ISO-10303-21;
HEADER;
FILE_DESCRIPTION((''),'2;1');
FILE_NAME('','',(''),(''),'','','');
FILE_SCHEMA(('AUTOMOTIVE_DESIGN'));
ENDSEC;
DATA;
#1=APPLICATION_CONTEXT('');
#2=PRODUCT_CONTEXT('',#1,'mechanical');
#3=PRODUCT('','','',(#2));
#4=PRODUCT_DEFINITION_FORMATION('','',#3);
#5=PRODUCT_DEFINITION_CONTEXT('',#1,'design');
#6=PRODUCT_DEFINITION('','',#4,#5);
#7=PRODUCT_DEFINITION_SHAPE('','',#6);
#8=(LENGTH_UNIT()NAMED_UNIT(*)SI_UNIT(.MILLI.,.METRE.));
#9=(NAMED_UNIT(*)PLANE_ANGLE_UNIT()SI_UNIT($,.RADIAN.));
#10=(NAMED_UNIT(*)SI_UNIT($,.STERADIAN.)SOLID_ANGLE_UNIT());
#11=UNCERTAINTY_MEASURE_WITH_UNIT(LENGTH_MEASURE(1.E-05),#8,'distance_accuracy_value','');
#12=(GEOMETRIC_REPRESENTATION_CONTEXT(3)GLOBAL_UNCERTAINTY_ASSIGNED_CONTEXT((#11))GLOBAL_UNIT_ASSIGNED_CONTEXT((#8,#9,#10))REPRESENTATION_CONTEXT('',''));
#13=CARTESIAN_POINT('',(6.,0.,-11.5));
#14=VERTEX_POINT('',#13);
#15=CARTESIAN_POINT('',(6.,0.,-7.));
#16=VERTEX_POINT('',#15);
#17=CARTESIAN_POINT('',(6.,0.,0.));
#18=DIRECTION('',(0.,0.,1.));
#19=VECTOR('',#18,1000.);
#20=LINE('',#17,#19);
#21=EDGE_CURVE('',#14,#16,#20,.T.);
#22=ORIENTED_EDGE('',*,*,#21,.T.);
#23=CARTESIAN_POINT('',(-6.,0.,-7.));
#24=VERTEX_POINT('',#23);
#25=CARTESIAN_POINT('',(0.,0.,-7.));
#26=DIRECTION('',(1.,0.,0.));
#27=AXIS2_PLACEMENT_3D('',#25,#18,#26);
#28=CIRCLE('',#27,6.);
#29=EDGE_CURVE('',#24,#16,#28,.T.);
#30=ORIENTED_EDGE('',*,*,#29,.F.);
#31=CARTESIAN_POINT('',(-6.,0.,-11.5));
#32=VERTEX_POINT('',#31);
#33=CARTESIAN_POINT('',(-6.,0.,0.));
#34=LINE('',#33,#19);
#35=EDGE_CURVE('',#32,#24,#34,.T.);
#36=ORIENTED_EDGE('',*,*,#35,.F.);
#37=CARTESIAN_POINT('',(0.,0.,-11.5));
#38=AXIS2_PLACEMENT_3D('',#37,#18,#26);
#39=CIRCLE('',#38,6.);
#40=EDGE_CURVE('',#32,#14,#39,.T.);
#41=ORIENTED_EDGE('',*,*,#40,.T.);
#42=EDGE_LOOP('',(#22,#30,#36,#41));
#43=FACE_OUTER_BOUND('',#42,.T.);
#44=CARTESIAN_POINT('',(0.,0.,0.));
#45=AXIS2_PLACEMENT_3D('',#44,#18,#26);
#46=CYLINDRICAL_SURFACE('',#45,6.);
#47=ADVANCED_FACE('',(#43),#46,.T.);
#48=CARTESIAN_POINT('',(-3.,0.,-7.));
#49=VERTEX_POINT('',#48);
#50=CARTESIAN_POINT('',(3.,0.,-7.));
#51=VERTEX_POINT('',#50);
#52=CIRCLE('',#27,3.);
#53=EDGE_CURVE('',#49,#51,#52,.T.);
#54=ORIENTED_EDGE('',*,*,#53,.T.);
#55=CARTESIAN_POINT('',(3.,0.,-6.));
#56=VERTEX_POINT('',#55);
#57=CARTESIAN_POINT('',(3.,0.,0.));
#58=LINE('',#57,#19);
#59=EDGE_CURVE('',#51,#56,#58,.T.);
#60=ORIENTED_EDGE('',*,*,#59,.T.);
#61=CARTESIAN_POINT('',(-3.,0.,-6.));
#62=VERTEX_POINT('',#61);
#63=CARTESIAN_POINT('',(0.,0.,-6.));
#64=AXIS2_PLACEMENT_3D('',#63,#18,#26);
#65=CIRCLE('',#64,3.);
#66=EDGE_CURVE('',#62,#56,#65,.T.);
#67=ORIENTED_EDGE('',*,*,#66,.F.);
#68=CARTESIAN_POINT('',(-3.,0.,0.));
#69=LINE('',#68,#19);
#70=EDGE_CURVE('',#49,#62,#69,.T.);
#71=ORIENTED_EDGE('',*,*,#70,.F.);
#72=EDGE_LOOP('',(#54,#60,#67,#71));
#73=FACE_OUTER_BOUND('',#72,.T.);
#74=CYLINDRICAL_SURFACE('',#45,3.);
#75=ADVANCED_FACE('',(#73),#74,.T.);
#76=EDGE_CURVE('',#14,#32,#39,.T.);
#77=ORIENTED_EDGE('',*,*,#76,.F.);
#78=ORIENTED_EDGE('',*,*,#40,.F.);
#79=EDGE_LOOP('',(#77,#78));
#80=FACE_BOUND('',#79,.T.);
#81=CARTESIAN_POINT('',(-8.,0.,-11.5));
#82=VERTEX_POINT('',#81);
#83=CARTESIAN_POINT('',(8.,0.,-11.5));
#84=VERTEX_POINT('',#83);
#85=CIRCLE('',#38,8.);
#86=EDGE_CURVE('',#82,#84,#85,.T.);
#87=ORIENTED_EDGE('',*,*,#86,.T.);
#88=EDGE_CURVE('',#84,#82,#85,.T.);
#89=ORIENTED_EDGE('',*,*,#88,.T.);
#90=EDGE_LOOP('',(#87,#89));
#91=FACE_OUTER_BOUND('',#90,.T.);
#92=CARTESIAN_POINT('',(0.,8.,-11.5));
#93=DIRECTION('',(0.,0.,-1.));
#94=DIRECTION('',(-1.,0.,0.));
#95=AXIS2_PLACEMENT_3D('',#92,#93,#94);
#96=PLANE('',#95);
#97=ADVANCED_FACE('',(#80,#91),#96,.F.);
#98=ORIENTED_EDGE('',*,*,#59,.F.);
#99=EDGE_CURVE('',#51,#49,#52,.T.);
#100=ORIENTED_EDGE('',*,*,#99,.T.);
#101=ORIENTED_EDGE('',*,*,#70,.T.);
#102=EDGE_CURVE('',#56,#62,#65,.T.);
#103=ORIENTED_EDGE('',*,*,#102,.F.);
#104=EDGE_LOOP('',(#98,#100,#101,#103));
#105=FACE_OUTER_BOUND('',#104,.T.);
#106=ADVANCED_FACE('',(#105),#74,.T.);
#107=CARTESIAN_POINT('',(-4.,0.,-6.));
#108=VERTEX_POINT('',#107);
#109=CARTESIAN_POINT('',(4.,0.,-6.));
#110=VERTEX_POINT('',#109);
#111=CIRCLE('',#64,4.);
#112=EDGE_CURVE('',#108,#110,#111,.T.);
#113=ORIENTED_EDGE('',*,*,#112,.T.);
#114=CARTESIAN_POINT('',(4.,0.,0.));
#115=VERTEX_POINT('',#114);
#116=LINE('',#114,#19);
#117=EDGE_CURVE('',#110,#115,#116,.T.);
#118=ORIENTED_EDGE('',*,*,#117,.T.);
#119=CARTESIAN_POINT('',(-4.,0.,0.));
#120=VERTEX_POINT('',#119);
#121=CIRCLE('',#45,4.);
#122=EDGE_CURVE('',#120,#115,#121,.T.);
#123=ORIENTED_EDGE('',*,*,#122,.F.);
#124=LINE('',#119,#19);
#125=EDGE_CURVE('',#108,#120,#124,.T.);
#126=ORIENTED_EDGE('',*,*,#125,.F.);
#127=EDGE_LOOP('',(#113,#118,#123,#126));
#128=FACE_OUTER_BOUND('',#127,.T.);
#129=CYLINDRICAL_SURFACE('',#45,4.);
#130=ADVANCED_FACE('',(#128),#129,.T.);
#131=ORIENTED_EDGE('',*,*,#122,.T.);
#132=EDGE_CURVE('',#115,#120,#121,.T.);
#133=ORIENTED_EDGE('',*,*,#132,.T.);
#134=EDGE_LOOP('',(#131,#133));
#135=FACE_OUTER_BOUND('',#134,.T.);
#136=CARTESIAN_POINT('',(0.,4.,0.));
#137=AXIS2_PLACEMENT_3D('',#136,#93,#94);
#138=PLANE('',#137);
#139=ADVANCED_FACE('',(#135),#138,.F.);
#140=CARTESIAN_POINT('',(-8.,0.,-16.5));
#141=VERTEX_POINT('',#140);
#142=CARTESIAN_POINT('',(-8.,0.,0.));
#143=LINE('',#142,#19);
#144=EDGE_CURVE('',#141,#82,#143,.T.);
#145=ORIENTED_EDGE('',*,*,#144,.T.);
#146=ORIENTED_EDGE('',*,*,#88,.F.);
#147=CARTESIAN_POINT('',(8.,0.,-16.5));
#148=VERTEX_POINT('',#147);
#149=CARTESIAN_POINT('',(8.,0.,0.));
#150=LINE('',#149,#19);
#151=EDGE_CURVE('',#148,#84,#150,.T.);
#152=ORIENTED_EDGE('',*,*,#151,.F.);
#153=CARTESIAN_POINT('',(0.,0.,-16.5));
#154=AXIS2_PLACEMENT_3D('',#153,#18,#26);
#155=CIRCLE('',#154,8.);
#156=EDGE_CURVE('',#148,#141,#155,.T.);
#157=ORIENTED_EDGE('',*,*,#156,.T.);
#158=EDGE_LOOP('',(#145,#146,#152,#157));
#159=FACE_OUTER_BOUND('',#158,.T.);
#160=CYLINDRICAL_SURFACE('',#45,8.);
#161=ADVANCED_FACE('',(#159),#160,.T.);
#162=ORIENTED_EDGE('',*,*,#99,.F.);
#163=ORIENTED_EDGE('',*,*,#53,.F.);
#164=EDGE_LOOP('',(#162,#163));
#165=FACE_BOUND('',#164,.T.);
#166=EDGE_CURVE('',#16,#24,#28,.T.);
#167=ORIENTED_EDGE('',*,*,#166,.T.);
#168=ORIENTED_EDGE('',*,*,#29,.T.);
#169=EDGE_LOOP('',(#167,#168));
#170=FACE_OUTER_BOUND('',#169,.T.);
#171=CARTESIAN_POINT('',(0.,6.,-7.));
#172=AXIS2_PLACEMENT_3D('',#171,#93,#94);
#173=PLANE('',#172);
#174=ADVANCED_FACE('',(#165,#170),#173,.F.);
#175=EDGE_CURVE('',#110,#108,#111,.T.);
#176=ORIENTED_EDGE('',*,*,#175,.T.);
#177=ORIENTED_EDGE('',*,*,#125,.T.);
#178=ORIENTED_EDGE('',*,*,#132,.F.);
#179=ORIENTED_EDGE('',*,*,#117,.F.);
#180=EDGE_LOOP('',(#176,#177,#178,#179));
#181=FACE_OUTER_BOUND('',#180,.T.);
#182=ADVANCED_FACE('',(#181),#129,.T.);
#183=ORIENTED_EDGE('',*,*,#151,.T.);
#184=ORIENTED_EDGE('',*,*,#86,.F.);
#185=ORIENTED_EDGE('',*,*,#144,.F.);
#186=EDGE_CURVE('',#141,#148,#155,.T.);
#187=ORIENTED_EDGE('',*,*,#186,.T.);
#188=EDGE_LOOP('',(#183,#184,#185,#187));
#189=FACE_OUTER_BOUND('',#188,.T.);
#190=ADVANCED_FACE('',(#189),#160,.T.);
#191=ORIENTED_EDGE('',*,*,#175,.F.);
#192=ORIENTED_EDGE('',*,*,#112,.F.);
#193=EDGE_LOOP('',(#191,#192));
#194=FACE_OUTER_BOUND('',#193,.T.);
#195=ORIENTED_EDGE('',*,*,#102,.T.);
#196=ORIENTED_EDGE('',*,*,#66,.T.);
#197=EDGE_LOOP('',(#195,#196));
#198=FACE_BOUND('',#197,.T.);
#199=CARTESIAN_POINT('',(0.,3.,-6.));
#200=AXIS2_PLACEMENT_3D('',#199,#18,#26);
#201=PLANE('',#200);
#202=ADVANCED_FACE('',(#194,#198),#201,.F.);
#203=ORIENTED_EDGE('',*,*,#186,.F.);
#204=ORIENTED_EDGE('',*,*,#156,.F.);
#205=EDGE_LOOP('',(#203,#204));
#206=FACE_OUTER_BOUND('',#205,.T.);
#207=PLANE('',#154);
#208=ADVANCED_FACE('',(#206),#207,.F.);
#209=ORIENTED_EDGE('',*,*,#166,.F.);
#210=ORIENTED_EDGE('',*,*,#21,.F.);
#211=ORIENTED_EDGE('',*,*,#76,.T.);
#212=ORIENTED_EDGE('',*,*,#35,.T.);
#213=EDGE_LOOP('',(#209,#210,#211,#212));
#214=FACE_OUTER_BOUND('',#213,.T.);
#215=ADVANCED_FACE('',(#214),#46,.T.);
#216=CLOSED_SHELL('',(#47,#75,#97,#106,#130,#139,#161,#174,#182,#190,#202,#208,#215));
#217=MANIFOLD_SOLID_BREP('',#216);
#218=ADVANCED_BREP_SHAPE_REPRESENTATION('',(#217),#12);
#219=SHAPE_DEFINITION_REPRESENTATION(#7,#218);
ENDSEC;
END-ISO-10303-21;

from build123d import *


with BuildPart() as part:
    # Sketch1 → Revolve1 (revolve)
    with BuildSketch(Plane(origin=(0, 0, 0), x_dir=(0, 0, -1), z_dir=(1, 0, 0)), mode=Mode.PRIVATE) as revolve1_sk:
        Polygon((16.5, 0), (16.5, 8), (11.5, 8), (11.5, 6), (7, 6), (7, 3), (6, 3), (6, 4), (0, 4), (0, 0), align=None)
    revolve(revolve1_sk.sketch.rotate(Axis((0, 0, 0), (0, 0, -1)), 90), axis=Axis((0, 0, 0), (0, 0, -1)))


solid = part.part
